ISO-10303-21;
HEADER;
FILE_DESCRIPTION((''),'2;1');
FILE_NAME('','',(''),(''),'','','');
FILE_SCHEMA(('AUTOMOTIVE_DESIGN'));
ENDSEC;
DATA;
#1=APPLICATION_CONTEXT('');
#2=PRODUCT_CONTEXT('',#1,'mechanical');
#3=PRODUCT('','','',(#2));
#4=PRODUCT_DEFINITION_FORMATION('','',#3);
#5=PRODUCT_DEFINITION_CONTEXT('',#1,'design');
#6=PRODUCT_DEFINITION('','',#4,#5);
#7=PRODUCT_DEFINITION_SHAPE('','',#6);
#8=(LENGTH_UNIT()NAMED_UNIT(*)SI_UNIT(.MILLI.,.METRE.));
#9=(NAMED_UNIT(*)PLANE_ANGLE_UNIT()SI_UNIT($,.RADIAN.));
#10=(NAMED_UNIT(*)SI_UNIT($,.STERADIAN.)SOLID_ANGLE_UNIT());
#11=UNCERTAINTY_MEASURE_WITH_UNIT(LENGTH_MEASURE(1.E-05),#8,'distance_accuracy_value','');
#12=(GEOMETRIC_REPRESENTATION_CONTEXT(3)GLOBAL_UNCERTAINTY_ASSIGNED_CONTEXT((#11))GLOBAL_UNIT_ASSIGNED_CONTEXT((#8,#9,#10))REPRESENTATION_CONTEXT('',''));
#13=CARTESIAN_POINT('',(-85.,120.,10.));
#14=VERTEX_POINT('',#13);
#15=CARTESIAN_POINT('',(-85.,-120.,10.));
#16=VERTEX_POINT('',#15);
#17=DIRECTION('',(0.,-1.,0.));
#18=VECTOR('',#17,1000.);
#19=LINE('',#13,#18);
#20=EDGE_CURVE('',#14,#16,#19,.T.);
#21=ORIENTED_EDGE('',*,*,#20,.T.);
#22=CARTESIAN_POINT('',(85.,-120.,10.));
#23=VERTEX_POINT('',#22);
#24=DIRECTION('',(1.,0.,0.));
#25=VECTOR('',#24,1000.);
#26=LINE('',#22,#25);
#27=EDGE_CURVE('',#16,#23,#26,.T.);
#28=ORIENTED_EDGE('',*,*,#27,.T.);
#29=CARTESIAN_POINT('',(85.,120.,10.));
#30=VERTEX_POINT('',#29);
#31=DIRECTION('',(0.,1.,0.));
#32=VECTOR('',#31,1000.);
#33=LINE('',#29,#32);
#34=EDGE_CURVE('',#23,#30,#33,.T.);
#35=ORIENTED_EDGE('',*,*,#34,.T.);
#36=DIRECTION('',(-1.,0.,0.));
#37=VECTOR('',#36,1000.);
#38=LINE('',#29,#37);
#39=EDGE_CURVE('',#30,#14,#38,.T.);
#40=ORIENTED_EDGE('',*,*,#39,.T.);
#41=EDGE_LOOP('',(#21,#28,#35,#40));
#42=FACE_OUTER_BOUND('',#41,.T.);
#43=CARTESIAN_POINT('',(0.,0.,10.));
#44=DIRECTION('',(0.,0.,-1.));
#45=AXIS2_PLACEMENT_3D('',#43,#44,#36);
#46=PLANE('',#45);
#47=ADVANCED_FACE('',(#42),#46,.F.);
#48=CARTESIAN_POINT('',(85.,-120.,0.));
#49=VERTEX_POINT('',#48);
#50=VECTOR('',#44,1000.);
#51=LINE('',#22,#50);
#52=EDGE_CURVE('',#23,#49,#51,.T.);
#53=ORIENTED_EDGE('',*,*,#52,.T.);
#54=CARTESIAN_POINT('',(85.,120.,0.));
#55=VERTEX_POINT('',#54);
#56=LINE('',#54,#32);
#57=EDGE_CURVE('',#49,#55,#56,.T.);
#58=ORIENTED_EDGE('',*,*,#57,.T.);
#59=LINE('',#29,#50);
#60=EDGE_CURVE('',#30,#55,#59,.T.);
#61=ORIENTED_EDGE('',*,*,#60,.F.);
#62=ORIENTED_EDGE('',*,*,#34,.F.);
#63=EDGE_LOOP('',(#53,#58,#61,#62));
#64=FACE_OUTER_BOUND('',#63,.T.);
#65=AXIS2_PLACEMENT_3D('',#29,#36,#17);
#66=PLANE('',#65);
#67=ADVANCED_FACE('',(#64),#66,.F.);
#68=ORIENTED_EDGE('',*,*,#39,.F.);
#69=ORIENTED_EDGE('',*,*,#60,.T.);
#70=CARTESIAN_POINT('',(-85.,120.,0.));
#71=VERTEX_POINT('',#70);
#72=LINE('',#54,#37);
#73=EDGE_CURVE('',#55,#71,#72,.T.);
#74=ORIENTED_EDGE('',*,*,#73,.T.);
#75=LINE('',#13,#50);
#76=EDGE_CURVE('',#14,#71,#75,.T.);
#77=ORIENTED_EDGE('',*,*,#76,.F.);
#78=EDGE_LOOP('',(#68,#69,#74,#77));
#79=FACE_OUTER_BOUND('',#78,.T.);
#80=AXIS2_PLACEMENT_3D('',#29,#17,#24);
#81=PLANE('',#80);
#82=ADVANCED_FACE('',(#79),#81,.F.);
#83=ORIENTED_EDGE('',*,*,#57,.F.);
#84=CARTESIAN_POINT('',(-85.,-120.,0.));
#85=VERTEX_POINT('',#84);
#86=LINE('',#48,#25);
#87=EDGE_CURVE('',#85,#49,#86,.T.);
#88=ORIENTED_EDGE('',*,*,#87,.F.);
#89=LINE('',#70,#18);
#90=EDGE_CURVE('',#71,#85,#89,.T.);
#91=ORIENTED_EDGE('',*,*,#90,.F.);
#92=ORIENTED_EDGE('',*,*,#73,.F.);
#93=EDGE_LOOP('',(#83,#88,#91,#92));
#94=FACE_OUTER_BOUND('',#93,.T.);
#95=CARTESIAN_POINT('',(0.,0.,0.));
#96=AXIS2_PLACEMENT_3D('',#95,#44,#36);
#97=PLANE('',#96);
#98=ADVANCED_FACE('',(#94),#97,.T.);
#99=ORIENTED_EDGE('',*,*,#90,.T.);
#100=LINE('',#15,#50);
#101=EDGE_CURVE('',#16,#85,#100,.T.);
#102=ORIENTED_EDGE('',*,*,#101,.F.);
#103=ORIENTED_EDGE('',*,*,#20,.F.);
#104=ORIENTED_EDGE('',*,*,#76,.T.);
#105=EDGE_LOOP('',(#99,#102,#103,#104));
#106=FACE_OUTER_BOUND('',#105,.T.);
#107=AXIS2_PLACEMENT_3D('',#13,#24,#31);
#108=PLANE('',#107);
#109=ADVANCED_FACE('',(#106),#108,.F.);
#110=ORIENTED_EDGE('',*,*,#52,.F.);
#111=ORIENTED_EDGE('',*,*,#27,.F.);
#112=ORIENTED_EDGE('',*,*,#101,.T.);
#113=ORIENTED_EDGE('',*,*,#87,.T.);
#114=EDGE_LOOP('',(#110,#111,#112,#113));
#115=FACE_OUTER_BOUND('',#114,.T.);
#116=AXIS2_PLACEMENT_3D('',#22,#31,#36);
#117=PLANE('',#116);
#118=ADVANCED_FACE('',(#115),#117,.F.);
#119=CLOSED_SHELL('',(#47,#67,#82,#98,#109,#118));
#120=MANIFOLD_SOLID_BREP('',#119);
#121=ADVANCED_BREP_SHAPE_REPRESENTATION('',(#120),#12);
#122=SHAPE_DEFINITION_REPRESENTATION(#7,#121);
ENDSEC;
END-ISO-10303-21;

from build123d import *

# Parameters (mm, degrees)
SKETCH_1_W      = 170
SKETCH_1_H      = 240
EXTRUDE_1_DEPTH = 10


with BuildPart() as part:
    # 草图1 → 凸台-拉伸1 (new body)
    with BuildSketch(Plane.XY):
        Rectangle(SKETCH_1_W, SKETCH_1_H)
    extrude(amount=EXTRUDE_1_DEPTH)


solid = part.part
